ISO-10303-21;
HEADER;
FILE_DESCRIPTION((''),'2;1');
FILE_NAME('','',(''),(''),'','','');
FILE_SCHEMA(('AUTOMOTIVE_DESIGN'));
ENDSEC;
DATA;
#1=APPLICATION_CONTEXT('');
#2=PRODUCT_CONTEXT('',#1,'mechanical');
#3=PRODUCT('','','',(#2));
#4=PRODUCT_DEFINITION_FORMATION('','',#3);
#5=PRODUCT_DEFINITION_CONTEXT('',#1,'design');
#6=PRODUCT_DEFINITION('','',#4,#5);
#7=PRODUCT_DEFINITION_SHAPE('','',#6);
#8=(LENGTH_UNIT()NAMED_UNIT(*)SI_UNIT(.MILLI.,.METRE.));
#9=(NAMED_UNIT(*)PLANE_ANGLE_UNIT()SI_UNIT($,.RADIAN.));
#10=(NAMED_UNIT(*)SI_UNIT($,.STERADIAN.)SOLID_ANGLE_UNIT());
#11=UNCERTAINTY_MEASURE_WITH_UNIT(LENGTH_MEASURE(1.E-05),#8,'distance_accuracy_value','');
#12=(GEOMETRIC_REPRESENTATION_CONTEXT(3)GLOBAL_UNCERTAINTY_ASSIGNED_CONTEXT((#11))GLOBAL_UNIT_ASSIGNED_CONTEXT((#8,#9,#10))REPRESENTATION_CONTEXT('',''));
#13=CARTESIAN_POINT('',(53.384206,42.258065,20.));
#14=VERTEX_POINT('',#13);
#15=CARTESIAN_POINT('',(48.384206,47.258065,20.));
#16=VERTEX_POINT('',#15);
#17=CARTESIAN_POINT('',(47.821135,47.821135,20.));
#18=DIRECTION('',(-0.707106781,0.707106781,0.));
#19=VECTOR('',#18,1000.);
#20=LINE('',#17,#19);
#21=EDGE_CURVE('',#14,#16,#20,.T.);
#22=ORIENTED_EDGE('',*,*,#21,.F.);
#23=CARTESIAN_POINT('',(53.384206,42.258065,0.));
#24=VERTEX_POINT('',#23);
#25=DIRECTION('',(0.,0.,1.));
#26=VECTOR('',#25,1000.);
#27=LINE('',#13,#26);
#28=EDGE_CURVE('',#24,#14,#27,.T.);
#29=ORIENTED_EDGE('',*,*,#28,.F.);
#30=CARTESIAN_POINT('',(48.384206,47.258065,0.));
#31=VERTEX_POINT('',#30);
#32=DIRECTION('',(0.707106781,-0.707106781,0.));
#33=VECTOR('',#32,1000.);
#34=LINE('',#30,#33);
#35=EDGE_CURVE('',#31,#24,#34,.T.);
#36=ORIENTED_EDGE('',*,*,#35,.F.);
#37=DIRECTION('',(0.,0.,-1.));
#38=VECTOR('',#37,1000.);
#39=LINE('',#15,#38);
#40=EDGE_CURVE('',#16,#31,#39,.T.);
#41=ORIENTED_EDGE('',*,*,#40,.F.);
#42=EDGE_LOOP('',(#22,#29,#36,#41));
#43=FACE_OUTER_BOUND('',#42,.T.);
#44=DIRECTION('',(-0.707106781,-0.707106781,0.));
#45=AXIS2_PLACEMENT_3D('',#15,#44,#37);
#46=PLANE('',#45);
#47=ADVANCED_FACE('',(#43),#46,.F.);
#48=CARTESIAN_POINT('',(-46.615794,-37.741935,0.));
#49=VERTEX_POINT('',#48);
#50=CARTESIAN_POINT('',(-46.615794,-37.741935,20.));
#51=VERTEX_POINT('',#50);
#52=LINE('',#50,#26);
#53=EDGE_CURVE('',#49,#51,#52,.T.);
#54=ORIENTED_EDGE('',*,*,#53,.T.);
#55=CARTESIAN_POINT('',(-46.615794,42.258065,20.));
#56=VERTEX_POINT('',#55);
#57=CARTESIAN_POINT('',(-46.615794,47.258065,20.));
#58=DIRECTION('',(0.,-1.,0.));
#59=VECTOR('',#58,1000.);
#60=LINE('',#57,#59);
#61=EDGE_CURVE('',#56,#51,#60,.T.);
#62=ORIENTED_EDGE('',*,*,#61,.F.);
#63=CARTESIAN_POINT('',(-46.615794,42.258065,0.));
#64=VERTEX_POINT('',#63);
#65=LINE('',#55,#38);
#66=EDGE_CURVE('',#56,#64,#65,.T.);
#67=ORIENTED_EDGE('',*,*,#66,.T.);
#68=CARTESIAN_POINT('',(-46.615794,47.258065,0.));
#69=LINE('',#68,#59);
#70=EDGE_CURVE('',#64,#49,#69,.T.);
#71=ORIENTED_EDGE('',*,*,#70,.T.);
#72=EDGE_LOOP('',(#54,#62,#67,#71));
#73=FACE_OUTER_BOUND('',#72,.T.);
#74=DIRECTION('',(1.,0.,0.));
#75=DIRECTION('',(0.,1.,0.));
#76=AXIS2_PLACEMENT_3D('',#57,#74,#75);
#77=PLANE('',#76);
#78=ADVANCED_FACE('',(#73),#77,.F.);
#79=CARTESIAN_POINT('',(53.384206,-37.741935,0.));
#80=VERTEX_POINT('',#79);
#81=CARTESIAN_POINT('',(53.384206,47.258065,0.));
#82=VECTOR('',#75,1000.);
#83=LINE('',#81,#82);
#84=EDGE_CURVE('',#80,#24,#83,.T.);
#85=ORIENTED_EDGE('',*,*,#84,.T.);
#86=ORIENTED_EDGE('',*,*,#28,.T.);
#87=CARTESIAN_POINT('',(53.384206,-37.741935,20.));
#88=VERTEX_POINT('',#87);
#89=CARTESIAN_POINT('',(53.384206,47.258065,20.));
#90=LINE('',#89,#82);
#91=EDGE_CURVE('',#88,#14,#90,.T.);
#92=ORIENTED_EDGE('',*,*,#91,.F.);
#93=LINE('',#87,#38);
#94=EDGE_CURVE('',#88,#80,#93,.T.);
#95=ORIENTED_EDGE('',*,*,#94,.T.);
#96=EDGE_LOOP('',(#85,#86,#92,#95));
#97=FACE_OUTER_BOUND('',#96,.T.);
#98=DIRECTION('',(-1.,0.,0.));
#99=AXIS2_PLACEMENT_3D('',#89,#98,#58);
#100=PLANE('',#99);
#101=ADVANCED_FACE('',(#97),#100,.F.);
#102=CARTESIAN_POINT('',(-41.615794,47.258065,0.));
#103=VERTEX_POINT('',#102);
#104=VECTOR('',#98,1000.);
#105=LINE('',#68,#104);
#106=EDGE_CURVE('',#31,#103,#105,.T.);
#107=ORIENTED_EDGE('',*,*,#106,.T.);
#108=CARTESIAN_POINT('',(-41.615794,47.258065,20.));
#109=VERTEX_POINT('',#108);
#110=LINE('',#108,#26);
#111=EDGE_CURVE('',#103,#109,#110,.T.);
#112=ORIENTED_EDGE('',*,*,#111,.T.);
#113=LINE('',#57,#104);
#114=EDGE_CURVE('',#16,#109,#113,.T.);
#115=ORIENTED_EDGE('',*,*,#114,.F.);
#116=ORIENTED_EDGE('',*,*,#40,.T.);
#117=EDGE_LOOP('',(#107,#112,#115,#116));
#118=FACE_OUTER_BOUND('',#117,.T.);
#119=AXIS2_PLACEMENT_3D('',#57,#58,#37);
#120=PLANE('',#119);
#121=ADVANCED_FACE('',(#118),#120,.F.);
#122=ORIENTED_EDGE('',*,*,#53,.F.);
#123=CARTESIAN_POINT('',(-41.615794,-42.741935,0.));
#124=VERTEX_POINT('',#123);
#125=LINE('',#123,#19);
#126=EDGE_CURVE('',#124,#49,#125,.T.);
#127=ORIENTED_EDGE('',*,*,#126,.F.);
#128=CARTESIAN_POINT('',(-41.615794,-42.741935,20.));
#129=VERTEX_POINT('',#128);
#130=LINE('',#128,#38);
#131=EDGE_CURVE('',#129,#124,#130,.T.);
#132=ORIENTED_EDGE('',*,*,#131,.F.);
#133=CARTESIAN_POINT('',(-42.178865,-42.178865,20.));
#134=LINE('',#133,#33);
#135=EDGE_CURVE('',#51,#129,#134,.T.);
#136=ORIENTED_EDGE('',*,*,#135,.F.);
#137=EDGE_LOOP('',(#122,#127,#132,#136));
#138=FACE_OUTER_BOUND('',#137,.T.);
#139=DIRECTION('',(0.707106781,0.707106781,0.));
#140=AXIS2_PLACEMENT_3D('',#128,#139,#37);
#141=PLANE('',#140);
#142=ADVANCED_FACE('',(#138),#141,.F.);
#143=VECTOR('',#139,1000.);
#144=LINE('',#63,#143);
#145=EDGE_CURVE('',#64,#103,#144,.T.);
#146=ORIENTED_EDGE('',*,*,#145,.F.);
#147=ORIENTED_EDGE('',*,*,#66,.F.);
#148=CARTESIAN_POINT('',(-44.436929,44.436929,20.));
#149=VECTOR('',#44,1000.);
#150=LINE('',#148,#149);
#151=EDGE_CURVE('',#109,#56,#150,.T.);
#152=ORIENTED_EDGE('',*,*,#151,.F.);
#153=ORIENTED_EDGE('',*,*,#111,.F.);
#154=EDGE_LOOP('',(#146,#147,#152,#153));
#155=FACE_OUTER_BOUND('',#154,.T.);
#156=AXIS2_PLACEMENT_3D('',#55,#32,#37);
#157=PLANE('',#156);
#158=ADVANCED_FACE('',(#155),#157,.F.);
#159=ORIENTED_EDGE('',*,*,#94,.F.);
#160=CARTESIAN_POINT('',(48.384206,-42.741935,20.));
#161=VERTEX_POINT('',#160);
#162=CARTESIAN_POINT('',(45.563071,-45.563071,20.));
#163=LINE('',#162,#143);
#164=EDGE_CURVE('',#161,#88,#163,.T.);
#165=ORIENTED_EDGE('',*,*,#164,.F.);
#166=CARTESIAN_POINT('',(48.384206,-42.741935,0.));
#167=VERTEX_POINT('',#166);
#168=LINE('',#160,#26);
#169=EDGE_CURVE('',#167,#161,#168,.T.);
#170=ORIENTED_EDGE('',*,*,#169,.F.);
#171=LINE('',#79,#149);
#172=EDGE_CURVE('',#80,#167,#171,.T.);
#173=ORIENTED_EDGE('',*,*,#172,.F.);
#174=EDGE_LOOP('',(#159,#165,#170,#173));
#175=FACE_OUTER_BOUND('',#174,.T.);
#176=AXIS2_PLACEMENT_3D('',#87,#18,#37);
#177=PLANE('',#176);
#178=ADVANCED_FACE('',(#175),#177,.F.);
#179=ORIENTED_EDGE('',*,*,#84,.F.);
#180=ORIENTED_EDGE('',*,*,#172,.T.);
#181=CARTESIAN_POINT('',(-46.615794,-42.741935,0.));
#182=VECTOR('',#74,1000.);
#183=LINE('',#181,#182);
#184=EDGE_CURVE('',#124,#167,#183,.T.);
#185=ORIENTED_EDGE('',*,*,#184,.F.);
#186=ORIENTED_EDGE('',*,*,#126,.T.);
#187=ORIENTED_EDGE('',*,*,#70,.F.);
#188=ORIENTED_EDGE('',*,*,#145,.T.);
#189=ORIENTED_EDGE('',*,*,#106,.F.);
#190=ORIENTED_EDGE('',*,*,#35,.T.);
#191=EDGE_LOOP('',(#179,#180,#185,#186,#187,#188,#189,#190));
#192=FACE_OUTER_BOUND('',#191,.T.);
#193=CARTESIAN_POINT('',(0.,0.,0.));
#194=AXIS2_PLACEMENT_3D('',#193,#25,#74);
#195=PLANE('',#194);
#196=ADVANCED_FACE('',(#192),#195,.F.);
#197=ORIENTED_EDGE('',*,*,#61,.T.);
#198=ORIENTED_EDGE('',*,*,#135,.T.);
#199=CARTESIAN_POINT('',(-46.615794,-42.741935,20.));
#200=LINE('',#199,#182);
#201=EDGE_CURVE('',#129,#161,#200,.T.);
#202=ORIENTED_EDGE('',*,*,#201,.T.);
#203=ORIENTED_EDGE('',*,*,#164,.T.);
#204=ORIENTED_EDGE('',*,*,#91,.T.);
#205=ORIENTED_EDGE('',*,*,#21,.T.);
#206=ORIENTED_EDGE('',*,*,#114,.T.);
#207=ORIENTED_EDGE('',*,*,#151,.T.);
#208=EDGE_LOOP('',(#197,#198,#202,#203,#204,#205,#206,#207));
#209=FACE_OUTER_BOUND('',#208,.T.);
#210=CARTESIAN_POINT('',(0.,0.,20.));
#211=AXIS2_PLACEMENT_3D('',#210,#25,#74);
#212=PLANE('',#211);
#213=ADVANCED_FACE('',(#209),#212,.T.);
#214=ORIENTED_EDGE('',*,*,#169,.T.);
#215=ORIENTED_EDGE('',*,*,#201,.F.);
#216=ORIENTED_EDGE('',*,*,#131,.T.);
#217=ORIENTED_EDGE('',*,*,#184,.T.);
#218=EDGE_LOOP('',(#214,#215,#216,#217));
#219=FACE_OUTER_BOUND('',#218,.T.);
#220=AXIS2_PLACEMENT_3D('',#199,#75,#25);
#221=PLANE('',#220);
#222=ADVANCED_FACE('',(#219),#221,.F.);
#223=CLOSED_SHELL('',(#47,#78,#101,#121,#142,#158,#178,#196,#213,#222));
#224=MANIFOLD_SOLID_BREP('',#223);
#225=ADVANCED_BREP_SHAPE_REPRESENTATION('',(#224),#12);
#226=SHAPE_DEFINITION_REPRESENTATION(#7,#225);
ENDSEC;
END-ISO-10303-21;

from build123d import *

# Parameters (mm, degrees)
SKETCH1_W           = 100
SKETCH1_H           = 90
BOSS_EXTRUDE1_DEPTH = 20
CHAMFER1_SIZE       = 5


with BuildPart() as part:
    # Sketch1 → Boss-Extrude1 (new body)
    with BuildSketch(Plane.XY):
        with Locations((3.384206163, 2.258064516)):
            Rectangle(SKETCH1_W, SKETCH1_H)
    extrude(amount=BOSS_EXTRUDE1_DEPTH)

    # Chamfer1
    chamfer1_edges = [part.edges().sort_by_distance(p)[0] for p in [
        (-46.615793837, 47.258064516, 10),
        (53.384206163, 47.258064516, 10),
        (53.384206163, -42.741935484, 10),
        (-46.615793837, -42.741935484, 10),
    ]]
    chamfer(chamfer1_edges, length=CHAMFER1_SIZE)


solid = part.part
